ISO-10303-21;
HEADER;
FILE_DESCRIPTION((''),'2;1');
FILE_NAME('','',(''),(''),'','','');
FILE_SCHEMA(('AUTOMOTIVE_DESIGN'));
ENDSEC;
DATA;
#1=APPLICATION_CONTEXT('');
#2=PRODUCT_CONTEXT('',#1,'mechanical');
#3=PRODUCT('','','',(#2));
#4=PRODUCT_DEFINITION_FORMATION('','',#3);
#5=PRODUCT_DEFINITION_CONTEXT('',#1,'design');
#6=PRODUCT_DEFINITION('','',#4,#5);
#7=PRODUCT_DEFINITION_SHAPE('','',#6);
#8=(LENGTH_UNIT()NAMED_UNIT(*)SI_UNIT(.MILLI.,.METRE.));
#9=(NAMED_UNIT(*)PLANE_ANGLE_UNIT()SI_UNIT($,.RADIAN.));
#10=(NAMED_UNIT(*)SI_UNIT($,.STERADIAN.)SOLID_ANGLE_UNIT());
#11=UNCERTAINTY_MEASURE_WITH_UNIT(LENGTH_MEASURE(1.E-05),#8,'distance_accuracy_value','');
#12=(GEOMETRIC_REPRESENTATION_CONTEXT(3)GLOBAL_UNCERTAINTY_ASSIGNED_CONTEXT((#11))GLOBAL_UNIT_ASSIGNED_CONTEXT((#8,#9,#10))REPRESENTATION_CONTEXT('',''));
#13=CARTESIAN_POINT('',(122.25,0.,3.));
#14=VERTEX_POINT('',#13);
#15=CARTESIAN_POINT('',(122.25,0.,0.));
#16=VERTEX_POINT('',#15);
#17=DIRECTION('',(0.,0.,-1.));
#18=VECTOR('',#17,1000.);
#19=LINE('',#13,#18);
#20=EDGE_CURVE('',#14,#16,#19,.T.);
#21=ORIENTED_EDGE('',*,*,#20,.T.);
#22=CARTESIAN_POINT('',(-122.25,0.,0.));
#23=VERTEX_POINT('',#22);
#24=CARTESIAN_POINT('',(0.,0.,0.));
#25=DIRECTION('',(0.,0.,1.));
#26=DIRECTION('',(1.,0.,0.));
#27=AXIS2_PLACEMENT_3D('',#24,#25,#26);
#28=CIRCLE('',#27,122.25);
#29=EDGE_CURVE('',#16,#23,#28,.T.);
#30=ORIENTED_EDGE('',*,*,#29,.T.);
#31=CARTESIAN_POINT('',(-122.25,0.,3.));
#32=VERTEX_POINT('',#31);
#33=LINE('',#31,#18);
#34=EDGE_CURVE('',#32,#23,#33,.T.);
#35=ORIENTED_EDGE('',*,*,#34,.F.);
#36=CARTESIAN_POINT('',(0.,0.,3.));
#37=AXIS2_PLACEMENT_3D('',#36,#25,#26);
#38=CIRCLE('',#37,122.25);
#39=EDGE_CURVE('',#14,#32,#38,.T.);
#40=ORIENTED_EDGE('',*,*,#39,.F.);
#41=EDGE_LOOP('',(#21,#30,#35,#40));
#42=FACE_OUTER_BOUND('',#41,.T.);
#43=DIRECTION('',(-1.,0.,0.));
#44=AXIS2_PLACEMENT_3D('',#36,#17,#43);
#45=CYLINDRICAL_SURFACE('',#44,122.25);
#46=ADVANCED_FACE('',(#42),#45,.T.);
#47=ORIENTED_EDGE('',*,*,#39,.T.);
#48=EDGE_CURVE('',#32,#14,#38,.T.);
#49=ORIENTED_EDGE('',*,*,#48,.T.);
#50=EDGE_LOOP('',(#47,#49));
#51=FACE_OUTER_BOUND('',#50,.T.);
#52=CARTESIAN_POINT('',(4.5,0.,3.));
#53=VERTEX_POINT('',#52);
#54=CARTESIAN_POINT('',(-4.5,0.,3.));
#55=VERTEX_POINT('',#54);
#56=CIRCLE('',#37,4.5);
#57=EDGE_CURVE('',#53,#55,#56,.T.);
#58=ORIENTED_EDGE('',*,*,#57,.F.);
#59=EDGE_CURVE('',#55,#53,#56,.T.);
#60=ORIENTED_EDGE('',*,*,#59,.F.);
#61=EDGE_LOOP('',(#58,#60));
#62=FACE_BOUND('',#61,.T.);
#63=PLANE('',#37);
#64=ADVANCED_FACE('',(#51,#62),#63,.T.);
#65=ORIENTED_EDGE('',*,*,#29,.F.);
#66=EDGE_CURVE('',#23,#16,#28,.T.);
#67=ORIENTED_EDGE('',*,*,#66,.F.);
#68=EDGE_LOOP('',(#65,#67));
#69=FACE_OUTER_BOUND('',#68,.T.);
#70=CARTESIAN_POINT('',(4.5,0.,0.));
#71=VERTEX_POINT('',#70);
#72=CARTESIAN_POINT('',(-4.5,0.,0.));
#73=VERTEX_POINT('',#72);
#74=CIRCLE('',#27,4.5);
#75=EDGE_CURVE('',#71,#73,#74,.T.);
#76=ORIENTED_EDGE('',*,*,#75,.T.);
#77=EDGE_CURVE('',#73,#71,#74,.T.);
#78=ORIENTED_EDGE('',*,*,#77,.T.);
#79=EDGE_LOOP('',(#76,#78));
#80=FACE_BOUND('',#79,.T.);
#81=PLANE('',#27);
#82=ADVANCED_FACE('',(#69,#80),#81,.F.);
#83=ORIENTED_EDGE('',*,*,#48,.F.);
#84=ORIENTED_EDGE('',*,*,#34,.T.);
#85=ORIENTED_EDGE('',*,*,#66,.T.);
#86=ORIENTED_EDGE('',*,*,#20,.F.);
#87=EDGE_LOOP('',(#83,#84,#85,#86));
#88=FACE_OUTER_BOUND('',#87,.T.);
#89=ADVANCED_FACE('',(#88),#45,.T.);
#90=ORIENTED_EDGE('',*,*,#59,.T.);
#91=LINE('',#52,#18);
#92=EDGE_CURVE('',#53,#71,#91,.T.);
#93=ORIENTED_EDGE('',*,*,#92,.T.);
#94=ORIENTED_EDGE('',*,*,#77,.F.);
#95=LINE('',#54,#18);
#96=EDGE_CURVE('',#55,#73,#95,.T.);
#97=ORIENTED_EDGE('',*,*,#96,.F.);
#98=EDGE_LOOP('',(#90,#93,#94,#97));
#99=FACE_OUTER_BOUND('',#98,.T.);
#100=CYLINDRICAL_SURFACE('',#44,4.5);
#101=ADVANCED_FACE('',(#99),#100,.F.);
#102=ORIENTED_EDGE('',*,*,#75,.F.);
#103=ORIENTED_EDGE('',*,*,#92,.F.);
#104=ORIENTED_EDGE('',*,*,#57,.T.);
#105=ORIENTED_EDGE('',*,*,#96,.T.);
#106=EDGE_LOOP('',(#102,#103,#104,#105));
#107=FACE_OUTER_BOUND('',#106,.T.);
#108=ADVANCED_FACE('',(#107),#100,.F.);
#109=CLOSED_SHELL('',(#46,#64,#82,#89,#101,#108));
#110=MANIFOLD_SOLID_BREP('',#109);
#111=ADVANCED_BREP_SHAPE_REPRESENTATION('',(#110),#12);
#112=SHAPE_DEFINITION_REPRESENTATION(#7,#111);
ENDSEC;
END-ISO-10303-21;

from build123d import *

# Parameters (mm, degrees)
SKETCH_1_R      = 122.25
SKETCH_1_R_2    = 4.5
EXTRUDE_1_DEPTH = 3


with BuildPart() as part:
    # 草图1 → 凸台-拉伸1 (new body)
    with BuildSketch(Plane.XY):
        Circle(SKETCH_1_R)
        Circle(SKETCH_1_R_2, mode=Mode.SUBTRACT)
    extrude(amount=EXTRUDE_1_DEPTH)


solid = part.part
